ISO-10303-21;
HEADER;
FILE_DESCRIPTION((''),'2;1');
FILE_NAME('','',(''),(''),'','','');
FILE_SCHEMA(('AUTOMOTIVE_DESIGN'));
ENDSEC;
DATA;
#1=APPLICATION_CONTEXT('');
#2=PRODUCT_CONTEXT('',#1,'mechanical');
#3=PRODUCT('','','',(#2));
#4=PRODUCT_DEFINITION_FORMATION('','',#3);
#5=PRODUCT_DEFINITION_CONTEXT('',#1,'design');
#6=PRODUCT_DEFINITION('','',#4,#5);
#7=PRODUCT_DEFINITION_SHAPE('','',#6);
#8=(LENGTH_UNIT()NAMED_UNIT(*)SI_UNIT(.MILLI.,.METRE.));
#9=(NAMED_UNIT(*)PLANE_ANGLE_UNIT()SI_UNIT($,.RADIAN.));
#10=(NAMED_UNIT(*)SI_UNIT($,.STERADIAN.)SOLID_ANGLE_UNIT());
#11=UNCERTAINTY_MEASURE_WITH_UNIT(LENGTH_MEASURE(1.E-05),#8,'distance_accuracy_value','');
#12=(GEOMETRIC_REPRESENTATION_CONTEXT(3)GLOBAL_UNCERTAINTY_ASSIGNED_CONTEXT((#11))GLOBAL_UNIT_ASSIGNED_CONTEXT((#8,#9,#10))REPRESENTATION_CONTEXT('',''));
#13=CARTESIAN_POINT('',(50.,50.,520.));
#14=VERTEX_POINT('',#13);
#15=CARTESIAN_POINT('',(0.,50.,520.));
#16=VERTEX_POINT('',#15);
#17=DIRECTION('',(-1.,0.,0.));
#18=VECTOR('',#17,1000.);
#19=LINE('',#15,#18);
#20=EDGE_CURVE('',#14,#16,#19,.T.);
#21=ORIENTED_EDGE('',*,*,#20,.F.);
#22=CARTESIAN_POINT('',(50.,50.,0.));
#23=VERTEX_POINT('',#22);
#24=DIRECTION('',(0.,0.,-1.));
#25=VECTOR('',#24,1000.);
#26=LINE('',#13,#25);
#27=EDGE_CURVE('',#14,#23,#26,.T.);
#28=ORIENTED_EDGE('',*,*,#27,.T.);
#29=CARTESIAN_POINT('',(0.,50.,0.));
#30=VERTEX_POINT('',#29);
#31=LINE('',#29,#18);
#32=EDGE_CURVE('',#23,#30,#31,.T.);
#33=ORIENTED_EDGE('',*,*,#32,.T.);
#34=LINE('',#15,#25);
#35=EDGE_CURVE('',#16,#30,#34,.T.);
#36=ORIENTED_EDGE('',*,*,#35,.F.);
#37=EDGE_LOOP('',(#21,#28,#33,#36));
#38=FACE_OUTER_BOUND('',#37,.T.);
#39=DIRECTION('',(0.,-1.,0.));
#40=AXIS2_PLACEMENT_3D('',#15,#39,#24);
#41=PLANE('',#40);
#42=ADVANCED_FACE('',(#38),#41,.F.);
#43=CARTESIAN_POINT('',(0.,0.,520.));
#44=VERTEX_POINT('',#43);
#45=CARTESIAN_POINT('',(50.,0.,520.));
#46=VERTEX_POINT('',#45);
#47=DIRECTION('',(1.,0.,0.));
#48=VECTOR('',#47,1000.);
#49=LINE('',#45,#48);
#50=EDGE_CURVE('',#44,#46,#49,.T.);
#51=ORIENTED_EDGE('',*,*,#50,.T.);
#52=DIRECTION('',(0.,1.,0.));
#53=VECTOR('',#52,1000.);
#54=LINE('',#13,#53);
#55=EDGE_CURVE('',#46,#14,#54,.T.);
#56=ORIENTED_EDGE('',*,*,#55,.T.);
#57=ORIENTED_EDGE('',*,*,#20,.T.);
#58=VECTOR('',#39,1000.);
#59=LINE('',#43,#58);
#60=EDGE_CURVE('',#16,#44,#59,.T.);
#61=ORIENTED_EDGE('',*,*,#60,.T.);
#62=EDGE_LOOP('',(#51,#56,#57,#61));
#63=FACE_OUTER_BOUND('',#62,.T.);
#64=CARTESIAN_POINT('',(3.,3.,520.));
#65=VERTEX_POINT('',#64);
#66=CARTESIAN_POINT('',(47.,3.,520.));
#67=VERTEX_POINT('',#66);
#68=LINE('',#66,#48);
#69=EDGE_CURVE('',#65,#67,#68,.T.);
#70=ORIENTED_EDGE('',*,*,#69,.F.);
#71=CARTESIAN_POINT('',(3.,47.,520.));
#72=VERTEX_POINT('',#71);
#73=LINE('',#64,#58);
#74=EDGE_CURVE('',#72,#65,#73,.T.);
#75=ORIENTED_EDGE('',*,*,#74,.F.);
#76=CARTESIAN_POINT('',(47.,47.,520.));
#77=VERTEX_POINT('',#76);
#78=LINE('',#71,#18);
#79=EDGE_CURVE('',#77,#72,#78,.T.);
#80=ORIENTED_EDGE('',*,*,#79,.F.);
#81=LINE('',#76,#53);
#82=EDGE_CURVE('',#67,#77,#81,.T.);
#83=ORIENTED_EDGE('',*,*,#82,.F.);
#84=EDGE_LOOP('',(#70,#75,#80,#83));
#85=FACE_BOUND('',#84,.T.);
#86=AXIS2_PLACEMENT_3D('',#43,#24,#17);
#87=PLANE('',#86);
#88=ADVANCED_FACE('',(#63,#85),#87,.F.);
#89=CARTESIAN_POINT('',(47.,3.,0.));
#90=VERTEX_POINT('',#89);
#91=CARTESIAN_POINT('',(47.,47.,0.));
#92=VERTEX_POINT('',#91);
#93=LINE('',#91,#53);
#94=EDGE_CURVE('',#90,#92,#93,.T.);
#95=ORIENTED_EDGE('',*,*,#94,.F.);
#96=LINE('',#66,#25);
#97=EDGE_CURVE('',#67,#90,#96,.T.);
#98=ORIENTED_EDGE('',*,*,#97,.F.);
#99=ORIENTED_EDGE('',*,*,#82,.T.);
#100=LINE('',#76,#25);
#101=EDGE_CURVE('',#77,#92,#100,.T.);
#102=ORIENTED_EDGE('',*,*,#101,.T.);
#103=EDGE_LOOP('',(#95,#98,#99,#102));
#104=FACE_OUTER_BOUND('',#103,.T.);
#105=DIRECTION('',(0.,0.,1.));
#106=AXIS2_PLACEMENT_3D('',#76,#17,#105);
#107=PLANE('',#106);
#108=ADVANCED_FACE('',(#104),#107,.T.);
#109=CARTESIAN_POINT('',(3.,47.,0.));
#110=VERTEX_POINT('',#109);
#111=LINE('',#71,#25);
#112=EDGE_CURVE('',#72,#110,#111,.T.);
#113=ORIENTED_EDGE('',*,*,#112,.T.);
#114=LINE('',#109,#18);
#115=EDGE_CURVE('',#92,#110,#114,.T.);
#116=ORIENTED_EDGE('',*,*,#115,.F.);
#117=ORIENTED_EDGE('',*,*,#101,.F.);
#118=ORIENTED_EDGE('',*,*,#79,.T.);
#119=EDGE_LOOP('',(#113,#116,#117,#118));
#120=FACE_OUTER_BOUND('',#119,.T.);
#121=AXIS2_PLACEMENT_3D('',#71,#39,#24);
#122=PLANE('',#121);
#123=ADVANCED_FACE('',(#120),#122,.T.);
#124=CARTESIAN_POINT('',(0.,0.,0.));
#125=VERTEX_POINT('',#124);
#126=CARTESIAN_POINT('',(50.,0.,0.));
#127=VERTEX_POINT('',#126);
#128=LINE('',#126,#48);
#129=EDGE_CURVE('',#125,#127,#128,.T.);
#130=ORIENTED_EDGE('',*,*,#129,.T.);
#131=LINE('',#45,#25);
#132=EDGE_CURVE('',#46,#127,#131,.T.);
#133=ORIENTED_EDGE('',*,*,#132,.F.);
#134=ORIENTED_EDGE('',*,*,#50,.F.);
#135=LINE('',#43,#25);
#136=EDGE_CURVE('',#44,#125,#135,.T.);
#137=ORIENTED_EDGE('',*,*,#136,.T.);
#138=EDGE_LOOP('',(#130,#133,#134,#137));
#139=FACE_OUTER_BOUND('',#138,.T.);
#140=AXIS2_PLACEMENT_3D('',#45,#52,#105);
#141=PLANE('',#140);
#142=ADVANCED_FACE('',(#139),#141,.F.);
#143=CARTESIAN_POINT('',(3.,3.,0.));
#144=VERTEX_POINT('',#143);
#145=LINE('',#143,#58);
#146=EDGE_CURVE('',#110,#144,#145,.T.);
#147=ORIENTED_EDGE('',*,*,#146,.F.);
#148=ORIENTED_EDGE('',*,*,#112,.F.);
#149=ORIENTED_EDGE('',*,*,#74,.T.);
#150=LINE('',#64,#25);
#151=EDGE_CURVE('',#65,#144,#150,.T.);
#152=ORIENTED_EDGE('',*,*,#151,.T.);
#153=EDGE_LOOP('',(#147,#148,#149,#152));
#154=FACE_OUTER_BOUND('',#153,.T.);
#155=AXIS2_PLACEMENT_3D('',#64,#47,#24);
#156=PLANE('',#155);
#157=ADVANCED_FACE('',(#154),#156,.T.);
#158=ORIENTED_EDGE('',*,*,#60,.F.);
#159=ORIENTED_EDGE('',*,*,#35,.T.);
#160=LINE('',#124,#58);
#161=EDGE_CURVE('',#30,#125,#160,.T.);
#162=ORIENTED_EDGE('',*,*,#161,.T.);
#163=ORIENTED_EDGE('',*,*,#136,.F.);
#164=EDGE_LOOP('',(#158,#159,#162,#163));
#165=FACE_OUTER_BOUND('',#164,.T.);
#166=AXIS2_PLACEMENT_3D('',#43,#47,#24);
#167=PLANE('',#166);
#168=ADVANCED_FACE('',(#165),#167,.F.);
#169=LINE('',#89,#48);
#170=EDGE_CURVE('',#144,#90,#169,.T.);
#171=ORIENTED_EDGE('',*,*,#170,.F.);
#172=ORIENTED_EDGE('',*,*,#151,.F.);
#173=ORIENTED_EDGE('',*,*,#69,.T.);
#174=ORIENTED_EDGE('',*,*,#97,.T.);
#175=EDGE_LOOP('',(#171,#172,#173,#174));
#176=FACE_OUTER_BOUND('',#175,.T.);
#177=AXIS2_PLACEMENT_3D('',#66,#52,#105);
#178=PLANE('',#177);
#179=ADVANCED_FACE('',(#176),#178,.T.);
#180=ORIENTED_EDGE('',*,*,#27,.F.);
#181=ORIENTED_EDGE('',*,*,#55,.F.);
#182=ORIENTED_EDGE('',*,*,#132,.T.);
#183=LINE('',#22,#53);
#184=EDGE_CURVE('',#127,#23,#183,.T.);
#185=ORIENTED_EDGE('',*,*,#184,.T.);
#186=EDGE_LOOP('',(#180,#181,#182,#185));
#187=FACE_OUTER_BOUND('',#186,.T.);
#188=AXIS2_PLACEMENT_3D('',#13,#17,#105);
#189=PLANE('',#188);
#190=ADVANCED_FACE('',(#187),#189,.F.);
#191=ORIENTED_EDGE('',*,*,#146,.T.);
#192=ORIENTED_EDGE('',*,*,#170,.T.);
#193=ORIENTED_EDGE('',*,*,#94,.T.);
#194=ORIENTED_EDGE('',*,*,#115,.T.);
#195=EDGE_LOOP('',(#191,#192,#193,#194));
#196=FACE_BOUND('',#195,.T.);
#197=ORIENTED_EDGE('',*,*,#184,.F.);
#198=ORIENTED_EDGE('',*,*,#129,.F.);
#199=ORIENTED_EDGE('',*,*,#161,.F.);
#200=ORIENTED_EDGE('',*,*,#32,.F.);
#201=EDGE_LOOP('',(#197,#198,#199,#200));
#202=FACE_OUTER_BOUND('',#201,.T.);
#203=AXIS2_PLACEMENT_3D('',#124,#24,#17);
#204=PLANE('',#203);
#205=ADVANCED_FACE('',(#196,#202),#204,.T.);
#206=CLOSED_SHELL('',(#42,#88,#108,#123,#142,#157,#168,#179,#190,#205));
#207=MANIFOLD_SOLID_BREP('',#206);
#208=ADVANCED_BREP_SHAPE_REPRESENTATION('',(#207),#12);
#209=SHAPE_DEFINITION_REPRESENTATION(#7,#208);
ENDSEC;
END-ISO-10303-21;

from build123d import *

# Parameters (mm, degrees)
SKETCH_1_W      = 50
SKETCH_1_H      = 50
SKETCH_1_W_2    = 44
SKETCH_1_H_2    = 44
EXTRUDE_1_DEPTH = 520


with BuildPart() as part:
    # 草图1 → 凸台-拉伸1 (new body)
    with BuildSketch(Plane.XY):
        with Locations((25, 25)):
            Rectangle(SKETCH_1_W, SKETCH_1_H)
        with Locations((25, 25)):
            Rectangle(SKETCH_1_W_2, SKETCH_1_H_2, mode=Mode.SUBTRACT)
    extrude(amount=EXTRUDE_1_DEPTH)


solid = part.part
